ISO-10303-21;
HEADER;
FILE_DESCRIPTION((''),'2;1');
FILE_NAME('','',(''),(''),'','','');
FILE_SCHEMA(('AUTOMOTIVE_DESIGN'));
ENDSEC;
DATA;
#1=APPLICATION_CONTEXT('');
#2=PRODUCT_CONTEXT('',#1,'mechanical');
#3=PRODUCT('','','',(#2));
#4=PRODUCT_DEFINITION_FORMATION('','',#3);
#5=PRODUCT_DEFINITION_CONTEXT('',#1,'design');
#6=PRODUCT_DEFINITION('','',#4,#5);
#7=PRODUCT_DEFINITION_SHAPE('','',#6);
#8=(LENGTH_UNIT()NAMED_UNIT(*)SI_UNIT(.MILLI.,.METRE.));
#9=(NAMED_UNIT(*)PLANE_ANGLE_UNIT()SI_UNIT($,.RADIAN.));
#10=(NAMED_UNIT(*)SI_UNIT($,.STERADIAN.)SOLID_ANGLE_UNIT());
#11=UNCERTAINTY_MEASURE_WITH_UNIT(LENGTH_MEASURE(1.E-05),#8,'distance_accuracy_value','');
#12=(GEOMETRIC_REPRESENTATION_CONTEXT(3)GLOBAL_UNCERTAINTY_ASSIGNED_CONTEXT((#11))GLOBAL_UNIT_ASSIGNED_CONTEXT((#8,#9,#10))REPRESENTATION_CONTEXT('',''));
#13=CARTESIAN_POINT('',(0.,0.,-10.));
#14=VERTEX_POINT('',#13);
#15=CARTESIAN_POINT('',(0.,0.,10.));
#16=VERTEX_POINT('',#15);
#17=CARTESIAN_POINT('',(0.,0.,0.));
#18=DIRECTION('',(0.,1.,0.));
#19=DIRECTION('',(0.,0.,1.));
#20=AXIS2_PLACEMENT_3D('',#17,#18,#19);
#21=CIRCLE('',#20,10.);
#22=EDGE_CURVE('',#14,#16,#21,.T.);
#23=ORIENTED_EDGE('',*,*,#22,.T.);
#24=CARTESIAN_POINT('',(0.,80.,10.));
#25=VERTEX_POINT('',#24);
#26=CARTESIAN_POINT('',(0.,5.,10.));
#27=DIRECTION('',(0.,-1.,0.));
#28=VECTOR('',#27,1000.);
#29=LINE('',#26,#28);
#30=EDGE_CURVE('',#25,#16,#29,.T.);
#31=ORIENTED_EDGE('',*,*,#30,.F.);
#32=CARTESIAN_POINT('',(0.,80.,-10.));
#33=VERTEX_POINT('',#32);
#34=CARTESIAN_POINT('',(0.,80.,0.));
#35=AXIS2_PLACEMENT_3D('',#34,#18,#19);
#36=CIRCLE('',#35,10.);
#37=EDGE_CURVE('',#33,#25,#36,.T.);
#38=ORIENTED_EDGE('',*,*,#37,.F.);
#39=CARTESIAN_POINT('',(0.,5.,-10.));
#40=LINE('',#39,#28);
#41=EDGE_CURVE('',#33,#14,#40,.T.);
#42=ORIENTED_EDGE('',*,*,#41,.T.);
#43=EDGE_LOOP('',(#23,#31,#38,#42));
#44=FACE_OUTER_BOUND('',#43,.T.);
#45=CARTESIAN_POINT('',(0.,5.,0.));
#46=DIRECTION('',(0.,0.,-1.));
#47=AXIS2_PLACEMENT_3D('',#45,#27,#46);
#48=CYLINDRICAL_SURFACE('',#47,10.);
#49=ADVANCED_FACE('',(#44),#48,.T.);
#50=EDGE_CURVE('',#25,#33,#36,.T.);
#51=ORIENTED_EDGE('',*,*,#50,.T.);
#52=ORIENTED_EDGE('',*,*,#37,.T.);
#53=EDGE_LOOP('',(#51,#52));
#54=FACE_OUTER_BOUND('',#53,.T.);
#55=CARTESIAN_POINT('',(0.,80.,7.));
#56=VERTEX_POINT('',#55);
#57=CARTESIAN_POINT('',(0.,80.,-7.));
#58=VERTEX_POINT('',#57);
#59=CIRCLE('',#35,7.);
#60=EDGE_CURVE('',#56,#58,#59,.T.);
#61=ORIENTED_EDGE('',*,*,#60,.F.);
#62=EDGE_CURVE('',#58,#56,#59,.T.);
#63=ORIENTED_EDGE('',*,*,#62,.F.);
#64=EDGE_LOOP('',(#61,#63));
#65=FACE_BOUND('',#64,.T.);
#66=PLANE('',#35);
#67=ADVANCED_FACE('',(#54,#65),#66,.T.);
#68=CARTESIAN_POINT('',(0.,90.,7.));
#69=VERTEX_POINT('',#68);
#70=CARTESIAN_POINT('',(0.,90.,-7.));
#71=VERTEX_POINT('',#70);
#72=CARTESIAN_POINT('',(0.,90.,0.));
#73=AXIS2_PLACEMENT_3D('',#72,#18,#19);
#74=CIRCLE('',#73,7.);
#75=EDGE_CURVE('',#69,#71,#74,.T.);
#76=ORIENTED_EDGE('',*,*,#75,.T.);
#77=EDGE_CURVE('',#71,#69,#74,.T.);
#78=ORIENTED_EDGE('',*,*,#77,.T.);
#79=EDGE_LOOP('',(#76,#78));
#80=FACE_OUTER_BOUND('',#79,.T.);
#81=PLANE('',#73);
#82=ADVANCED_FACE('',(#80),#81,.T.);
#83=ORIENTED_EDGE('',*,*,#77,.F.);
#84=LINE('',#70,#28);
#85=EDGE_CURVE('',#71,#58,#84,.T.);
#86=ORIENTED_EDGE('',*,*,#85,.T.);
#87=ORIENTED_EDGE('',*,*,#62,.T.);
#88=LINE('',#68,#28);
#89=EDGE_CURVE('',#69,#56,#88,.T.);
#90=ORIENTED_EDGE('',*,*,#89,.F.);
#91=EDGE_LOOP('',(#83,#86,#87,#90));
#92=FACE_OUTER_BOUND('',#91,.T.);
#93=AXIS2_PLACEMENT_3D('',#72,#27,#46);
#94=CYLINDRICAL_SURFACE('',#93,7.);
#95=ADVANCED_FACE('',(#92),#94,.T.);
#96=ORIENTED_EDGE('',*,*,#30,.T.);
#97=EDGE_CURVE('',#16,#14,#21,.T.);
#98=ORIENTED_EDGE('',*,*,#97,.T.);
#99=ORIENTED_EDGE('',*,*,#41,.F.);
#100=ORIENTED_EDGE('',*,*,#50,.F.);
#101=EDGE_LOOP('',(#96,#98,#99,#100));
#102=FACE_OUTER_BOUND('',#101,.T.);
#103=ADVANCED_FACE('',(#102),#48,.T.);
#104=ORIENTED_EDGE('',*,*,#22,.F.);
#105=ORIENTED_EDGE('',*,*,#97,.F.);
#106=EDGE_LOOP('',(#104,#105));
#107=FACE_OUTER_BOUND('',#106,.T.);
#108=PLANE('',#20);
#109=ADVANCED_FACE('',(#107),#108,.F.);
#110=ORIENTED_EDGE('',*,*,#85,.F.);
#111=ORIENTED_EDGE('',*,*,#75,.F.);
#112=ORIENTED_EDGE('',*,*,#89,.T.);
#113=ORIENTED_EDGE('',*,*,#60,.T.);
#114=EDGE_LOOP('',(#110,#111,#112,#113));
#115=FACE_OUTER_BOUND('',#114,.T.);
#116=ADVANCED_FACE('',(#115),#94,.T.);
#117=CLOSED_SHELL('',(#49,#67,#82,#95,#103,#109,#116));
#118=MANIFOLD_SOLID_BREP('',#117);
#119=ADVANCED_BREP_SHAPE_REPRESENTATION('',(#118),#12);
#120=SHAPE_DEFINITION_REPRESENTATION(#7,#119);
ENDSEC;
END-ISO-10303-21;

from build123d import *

# Parameters (mm, degrees)
SKETCH1_R           = 10
BOSS_EXTRUDE1_DEPTH = 5
SKETCH2_R           = 10
BOSS_EXTRUDE2_DEPTH = 75
SKETCH3_R           = 7
BOSS_EXTRUDE3_DEPTH = 10


with BuildPart() as part:
    # Sketch1 → Boss-Extrude1 (new body)
    with BuildSketch(Plane(origin=(0, 0, 0), x_dir=(1, 0, 0), z_dir=(0, 1, 0))):
        with Locations(Location((0, 0, 0), (0, 0, 270))):
            Circle(SKETCH1_R)
    extrude(amount=BOSS_EXTRUDE1_DEPTH)

    # Sketch2 → Boss-Extrude2 (add)
    with BuildSketch(Plane(origin=(0, 5, 0), x_dir=(1, 0, 0), z_dir=(0, 1, 0))):
        with Locations(Location((0, 0, 0), (0, 0, 270))):
            Circle(SKETCH2_R)
    extrude(amount=BOSS_EXTRUDE2_DEPTH)

    # Sketch3 → Boss-Extrude3 (add)
    with BuildSketch(Plane(origin=(0, 80, 0), x_dir=(1, 0, 0), z_dir=(0, 1, 0))):
        with Locations(Location((0, 0, 0), (0, 0, 270))):
            Circle(SKETCH3_R)
    extrude(amount=BOSS_EXTRUDE3_DEPTH)


solid = part.part
